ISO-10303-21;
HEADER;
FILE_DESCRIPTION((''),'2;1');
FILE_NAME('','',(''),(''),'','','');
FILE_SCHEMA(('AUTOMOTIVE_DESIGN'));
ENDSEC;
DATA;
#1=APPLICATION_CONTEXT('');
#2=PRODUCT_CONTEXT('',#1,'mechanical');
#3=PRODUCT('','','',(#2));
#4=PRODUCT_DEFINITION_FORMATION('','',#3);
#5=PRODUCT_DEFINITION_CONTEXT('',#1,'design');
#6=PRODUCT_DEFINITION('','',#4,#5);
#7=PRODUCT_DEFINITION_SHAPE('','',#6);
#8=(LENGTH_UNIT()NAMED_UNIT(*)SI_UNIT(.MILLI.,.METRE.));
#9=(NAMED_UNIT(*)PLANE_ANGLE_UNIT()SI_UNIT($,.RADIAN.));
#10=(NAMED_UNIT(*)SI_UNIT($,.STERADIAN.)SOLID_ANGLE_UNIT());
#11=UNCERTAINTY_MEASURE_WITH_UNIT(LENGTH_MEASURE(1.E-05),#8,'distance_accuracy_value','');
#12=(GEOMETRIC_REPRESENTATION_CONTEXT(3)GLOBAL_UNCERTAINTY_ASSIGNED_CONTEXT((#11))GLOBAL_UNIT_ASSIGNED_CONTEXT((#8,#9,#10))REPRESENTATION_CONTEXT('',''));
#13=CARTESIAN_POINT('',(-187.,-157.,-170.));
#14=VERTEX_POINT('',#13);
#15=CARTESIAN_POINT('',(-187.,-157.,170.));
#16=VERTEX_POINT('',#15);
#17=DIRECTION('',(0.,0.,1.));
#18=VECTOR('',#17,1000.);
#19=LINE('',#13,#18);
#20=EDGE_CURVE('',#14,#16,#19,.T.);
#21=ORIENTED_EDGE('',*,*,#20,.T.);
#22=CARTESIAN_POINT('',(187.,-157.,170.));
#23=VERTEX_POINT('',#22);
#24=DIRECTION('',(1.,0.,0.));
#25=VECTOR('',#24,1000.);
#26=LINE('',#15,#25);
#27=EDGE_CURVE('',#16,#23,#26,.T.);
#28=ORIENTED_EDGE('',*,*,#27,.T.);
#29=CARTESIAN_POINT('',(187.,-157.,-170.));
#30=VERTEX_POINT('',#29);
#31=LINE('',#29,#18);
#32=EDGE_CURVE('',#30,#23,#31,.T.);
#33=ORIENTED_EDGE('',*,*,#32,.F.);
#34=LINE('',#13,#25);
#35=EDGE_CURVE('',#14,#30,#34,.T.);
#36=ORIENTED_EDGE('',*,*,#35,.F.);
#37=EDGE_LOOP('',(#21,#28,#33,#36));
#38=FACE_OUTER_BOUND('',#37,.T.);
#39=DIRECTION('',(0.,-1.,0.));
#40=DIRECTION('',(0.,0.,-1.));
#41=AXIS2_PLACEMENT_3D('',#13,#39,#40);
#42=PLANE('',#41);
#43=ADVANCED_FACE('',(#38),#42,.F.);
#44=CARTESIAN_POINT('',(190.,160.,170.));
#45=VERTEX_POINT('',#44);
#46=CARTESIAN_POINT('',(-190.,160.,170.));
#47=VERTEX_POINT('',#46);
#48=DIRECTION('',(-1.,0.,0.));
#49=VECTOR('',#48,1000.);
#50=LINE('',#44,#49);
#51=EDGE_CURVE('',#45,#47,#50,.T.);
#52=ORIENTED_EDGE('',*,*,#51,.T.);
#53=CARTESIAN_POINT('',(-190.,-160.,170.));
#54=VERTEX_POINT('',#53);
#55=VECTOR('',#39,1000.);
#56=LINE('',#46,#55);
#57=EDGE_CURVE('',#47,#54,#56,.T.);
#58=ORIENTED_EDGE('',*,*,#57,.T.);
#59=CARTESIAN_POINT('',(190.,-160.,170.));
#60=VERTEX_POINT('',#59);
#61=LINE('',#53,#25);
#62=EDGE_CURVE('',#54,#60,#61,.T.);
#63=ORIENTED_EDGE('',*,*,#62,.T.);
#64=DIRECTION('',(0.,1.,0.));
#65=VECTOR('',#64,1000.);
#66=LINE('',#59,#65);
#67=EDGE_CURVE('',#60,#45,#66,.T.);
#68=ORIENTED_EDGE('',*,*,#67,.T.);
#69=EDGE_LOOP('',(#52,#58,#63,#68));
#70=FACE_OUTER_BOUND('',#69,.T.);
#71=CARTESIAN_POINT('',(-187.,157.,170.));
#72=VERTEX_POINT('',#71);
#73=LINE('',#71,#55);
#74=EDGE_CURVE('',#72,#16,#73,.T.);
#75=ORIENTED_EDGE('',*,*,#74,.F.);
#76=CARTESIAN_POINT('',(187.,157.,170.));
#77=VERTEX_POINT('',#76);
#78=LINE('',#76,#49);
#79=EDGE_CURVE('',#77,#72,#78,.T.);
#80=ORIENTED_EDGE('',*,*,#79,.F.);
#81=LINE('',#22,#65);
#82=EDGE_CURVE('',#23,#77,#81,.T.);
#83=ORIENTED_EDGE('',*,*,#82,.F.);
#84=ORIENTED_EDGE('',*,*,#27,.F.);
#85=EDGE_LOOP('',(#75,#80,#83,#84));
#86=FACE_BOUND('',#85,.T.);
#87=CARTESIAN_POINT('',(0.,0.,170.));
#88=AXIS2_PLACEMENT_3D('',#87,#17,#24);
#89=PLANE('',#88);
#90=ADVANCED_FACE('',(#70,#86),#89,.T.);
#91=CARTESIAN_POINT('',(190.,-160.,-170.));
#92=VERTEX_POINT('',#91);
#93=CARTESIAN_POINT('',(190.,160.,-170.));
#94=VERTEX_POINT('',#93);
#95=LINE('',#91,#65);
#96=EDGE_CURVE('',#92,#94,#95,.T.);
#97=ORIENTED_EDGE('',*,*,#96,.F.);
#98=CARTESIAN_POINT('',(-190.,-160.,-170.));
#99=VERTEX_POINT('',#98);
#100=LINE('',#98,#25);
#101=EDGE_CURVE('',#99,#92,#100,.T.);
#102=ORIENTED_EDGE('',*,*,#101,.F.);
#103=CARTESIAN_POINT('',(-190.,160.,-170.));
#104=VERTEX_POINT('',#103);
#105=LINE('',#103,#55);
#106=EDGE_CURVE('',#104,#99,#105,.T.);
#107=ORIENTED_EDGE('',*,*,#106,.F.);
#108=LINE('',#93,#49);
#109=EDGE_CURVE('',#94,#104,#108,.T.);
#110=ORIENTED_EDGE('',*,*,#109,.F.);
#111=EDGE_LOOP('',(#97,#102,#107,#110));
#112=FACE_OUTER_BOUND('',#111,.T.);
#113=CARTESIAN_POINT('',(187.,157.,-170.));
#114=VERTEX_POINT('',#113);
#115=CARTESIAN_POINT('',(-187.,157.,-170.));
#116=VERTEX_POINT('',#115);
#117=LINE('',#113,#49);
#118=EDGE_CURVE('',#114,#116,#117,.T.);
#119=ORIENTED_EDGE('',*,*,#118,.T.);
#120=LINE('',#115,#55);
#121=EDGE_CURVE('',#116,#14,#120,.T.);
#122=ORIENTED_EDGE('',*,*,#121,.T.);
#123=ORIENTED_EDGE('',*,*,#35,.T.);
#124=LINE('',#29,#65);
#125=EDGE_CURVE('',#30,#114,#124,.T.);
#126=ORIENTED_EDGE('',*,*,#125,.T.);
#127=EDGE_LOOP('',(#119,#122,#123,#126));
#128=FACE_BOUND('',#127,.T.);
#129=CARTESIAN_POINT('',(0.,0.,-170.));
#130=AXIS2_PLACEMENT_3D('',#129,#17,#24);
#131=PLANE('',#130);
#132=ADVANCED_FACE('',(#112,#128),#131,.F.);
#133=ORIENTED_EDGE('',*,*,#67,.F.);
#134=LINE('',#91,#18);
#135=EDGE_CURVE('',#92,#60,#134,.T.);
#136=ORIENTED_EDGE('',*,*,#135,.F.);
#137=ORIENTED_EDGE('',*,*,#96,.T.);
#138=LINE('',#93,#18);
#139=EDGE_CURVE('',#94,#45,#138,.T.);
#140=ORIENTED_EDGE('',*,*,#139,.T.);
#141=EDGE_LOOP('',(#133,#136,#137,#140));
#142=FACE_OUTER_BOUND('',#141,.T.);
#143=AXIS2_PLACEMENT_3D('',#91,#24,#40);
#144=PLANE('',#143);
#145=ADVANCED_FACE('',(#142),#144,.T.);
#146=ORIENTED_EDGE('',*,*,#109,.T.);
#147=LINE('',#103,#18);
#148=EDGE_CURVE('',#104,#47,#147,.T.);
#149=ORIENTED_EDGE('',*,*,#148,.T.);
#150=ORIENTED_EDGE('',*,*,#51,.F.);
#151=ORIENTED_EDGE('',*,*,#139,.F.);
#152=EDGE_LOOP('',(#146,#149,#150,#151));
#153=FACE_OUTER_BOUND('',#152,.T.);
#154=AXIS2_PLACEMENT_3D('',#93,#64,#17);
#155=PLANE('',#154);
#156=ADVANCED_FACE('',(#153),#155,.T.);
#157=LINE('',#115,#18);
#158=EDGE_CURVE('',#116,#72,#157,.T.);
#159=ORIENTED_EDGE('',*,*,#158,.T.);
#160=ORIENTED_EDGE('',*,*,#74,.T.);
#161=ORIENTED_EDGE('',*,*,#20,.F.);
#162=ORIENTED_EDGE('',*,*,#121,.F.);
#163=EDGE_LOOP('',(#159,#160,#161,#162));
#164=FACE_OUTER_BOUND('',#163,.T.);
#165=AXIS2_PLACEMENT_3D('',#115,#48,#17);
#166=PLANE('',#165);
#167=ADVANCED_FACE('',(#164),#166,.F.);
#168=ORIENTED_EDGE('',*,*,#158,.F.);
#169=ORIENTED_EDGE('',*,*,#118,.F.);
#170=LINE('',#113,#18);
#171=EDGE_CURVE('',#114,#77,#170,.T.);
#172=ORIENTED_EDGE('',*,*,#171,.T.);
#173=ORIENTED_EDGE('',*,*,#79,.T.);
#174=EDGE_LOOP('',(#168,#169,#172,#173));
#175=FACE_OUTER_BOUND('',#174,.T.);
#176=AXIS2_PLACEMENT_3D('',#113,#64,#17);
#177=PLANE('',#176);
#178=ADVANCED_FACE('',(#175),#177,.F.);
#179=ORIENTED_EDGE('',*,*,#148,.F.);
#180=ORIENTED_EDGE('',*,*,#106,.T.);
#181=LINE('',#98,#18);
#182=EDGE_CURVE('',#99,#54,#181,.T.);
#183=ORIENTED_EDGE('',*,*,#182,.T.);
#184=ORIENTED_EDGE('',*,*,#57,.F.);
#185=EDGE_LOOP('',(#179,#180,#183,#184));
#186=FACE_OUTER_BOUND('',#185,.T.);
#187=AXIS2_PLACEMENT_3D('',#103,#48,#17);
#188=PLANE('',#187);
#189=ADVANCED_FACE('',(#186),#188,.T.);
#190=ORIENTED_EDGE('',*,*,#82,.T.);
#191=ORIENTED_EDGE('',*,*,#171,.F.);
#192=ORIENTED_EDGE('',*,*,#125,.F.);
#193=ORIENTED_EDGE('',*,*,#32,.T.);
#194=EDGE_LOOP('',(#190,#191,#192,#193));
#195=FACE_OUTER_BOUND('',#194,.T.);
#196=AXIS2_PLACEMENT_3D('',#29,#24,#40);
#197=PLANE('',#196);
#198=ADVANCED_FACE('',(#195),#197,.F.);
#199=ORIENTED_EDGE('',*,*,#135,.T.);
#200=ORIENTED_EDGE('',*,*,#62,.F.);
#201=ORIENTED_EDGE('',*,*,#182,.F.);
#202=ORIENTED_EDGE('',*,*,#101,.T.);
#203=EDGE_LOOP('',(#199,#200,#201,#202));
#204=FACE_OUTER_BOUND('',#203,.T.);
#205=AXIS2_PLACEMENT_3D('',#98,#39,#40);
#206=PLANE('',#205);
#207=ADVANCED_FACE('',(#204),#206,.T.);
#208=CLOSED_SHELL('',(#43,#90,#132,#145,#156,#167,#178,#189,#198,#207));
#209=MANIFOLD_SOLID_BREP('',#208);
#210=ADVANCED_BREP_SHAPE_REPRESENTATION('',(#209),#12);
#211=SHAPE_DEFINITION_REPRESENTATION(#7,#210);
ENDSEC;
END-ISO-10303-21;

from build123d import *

# Parameters (mm, degrees)
SKETCH_1_W      = 380
SKETCH_1_H      = 320
SKETCH_1_W_2    = 374
SKETCH_1_H_2    = 314
EXTRUDE_1_DEPTH = 170


with BuildPart() as part:
    # 草图1 → 凸台-拉伸1 (new, symmetric)
    with BuildSketch(Plane.XY):
        Rectangle(SKETCH_1_W, SKETCH_1_H)
        Rectangle(SKETCH_1_W_2, SKETCH_1_H_2, mode=Mode.SUBTRACT)
    extrude(amount=EXTRUDE_1_DEPTH, both=True)


solid = part.part
